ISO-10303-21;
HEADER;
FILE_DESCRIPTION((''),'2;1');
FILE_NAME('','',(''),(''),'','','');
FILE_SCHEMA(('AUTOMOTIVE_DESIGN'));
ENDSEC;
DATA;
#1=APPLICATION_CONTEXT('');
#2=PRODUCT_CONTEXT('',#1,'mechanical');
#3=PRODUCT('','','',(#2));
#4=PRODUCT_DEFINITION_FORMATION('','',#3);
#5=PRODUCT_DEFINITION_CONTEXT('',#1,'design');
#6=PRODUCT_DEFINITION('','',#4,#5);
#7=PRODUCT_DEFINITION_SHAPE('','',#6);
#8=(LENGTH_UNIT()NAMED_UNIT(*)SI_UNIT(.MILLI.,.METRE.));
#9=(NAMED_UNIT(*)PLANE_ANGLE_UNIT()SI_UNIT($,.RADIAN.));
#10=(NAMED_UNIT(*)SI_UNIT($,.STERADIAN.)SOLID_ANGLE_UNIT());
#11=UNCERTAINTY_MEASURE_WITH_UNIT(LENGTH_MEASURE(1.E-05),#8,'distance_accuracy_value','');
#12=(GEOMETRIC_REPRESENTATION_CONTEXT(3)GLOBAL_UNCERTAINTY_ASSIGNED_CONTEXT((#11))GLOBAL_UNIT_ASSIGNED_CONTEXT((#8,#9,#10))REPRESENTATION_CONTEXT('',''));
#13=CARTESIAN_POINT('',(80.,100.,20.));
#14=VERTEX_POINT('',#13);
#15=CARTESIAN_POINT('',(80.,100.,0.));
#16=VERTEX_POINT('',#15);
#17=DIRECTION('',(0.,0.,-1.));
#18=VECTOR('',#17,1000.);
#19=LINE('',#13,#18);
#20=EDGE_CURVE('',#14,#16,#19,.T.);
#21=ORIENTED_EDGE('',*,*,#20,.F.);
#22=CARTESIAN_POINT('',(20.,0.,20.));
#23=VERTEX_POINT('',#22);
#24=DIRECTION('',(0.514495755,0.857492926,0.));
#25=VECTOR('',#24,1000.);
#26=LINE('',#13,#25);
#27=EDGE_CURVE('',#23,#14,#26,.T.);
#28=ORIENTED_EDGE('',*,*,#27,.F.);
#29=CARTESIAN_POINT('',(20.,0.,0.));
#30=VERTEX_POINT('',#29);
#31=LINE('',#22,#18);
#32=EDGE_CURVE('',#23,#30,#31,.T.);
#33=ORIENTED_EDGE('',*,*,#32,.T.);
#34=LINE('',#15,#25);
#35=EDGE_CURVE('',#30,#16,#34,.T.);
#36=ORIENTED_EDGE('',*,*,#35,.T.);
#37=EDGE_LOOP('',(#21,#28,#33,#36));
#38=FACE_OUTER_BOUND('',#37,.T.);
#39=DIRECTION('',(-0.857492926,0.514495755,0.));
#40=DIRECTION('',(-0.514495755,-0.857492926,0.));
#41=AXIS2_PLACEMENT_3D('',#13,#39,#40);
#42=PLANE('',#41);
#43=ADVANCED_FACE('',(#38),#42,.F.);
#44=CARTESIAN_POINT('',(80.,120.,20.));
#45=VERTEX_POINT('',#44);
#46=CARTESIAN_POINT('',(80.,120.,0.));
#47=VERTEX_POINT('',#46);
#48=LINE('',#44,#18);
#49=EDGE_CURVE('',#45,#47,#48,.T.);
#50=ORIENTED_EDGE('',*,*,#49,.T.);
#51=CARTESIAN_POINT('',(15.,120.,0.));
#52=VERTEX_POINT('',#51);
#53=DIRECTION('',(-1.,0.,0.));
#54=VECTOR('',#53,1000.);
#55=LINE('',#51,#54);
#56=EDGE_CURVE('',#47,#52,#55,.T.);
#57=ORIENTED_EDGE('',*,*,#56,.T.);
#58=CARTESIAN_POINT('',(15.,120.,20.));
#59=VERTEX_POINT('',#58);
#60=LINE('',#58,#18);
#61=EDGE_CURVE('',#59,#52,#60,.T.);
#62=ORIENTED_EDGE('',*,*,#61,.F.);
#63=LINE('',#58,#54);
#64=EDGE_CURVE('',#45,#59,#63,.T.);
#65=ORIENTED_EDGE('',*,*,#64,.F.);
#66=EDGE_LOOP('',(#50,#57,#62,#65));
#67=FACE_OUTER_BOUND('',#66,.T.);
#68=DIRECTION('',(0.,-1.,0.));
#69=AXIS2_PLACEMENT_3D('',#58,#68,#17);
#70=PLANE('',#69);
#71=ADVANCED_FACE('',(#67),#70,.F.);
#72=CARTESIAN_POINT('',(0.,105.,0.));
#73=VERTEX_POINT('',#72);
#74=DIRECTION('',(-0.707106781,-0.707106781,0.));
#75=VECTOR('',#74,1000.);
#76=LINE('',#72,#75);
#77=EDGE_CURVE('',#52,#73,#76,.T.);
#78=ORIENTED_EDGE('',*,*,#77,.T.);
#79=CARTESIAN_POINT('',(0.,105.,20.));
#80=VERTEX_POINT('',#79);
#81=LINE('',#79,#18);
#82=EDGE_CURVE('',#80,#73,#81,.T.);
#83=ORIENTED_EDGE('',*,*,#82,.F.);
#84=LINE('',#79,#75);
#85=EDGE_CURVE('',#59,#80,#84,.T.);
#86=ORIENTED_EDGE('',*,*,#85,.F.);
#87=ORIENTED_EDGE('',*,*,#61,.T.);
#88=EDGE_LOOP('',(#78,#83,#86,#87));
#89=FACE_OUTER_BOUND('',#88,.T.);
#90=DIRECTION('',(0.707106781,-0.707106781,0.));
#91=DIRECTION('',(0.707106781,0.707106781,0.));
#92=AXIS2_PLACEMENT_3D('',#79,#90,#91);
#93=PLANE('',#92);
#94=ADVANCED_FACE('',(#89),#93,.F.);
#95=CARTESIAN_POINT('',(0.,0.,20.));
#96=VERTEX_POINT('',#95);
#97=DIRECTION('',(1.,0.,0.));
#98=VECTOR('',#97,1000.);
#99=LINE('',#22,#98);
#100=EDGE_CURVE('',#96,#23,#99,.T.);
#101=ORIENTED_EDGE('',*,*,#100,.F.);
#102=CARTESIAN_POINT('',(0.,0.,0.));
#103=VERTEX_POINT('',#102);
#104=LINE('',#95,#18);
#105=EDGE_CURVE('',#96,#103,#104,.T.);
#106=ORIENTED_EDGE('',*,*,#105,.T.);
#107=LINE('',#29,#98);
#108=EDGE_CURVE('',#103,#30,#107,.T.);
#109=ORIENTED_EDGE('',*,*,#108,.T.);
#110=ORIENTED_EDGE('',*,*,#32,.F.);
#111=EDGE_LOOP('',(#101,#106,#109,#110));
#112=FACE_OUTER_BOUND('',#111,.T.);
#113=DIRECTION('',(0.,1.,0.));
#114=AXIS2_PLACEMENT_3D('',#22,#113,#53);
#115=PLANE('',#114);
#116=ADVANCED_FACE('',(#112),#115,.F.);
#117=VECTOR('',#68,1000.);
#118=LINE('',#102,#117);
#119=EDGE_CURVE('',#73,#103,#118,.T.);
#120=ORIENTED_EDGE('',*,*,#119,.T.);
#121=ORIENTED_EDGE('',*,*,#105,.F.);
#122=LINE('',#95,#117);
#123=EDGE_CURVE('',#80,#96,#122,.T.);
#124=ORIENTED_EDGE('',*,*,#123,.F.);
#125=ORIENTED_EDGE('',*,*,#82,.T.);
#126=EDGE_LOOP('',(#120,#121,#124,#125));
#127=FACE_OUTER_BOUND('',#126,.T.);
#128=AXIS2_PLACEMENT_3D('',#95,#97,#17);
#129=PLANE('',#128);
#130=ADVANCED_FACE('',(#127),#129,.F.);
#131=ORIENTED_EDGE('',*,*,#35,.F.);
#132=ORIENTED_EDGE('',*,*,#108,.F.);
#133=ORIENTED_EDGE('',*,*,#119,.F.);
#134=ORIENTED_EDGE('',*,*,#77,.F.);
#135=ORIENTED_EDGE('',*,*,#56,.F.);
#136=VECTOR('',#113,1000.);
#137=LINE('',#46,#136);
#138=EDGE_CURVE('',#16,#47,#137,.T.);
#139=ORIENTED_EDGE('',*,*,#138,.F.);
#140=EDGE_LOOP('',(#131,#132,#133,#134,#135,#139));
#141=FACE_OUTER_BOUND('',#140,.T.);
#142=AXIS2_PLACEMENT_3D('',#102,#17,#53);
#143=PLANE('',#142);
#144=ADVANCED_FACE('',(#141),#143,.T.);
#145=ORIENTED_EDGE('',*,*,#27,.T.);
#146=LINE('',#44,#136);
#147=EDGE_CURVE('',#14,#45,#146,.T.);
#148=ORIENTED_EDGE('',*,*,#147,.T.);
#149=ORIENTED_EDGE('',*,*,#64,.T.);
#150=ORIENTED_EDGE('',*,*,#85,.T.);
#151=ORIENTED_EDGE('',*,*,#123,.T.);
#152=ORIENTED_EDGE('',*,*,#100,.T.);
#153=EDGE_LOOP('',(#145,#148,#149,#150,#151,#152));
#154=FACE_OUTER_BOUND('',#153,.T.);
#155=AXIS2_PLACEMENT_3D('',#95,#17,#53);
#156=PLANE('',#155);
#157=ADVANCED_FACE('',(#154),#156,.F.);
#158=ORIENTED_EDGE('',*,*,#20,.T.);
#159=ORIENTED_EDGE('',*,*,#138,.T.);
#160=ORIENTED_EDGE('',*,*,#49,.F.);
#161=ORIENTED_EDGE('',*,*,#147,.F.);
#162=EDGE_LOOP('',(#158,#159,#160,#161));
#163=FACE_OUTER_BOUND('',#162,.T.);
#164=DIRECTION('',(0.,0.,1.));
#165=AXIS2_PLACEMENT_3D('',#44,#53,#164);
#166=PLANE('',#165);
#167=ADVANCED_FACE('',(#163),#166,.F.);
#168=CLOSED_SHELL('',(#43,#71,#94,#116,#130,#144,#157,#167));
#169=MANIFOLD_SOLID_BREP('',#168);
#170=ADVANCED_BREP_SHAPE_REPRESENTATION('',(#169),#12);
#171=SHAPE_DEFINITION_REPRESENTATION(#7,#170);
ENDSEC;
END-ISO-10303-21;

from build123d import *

# Parameters (mm, degrees)
BOSS_EXTRUDE1_DEPTH = 20


with BuildPart() as part:
    # Sketch1 → Boss-Extrude1 (new body)
    with BuildSketch(Plane.XY):
        Polygon((0, 0), (0, 105), (15, 120), (80, 120), (80, 100), (20, 0), align=None)
    extrude(amount=BOSS_EXTRUDE1_DEPTH)


solid = part.part
